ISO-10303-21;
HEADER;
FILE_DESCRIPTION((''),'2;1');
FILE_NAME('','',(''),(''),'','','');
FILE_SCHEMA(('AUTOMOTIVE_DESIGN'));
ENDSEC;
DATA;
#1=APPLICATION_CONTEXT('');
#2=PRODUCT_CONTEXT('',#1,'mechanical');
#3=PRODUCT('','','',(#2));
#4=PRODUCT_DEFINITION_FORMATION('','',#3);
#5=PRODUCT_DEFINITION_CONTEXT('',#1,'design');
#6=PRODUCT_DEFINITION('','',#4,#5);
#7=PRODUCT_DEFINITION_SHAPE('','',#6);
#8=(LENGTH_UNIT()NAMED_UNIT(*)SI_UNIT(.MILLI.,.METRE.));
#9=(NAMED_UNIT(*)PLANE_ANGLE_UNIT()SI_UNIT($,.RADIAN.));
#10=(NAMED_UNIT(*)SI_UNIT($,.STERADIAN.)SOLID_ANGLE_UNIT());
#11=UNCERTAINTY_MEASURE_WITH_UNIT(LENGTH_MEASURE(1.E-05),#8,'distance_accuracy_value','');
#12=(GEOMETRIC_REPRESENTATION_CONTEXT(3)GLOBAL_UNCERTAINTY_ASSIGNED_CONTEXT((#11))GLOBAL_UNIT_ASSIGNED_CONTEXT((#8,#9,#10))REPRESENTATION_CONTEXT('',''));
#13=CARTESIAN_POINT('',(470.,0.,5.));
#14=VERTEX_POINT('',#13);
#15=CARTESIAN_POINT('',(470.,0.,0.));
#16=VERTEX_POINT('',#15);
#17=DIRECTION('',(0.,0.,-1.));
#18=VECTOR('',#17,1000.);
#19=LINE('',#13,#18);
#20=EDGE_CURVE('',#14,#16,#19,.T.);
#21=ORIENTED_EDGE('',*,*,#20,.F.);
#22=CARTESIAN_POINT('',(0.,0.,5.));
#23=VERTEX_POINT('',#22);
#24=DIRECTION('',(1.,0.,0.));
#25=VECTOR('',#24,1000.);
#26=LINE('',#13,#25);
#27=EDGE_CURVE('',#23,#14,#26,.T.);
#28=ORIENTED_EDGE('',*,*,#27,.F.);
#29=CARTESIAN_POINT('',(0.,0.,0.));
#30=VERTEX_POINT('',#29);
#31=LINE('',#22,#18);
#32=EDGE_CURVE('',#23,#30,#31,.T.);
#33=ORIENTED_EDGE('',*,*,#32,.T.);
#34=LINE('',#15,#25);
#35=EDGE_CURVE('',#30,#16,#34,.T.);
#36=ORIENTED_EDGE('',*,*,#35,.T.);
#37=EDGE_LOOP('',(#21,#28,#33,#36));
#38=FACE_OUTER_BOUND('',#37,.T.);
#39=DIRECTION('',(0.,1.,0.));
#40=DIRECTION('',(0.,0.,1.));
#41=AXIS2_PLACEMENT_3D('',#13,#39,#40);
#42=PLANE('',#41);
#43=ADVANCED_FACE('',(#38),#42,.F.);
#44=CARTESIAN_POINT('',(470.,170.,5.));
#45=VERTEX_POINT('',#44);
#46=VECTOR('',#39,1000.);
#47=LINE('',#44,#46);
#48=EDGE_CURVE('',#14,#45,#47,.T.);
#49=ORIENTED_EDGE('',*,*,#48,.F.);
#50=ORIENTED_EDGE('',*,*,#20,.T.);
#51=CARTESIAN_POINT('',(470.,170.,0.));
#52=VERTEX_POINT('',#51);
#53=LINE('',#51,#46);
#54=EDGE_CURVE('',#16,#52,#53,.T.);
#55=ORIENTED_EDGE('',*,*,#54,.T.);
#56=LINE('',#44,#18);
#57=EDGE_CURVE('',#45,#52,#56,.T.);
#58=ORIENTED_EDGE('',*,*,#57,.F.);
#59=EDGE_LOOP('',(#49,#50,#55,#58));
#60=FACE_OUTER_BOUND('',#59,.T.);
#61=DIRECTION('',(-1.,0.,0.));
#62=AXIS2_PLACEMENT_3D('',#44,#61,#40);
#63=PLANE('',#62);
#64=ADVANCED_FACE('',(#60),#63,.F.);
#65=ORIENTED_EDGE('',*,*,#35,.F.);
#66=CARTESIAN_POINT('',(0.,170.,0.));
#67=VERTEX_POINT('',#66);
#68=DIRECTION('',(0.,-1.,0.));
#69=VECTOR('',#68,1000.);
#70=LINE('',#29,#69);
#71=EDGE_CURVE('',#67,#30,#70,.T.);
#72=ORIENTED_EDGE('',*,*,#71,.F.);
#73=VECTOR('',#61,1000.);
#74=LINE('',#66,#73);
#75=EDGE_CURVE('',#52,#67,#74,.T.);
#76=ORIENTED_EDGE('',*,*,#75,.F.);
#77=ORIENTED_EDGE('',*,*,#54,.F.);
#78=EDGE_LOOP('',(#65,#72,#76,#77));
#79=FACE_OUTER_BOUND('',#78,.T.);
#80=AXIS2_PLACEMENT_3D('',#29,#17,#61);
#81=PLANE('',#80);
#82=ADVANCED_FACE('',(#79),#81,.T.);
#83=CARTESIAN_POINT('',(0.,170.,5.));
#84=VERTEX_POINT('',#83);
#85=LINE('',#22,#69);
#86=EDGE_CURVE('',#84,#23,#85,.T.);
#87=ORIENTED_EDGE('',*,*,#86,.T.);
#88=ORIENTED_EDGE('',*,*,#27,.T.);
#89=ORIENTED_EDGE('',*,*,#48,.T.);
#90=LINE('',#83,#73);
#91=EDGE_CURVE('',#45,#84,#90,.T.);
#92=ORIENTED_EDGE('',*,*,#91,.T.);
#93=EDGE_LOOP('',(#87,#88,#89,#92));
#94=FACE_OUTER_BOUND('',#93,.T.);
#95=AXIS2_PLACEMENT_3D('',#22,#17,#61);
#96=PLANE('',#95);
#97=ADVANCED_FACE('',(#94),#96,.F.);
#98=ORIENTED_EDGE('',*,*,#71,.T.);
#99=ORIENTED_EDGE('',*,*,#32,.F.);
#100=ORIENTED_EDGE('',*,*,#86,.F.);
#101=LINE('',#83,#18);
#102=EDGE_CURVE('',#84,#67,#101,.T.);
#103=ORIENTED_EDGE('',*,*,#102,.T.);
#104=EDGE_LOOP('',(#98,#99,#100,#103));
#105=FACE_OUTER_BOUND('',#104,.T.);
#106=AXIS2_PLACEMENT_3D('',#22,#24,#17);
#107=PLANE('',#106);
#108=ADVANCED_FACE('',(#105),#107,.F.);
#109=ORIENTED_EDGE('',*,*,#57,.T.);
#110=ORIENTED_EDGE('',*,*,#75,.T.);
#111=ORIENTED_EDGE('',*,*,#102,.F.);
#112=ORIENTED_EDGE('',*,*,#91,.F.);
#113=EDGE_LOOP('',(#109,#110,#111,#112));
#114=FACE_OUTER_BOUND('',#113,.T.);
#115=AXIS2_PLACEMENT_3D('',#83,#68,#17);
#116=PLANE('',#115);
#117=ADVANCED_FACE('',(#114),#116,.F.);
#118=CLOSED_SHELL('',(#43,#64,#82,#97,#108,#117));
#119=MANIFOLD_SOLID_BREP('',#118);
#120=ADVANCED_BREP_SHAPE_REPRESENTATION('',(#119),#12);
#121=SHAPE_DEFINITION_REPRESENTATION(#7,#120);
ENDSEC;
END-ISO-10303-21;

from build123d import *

# Parameters (mm, degrees)
SKETCH_1_W      = 470
SKETCH_1_H      = 170
EXTRUDE_1_DEPTH = 5


with BuildPart() as part:
    # 草图1 → 凸台-拉伸1 (new body)
    with BuildSketch(Plane.XY):
        with Locations((235, 85)):
            Rectangle(SKETCH_1_W, SKETCH_1_H)
    extrude(amount=EXTRUDE_1_DEPTH)


solid = part.part
